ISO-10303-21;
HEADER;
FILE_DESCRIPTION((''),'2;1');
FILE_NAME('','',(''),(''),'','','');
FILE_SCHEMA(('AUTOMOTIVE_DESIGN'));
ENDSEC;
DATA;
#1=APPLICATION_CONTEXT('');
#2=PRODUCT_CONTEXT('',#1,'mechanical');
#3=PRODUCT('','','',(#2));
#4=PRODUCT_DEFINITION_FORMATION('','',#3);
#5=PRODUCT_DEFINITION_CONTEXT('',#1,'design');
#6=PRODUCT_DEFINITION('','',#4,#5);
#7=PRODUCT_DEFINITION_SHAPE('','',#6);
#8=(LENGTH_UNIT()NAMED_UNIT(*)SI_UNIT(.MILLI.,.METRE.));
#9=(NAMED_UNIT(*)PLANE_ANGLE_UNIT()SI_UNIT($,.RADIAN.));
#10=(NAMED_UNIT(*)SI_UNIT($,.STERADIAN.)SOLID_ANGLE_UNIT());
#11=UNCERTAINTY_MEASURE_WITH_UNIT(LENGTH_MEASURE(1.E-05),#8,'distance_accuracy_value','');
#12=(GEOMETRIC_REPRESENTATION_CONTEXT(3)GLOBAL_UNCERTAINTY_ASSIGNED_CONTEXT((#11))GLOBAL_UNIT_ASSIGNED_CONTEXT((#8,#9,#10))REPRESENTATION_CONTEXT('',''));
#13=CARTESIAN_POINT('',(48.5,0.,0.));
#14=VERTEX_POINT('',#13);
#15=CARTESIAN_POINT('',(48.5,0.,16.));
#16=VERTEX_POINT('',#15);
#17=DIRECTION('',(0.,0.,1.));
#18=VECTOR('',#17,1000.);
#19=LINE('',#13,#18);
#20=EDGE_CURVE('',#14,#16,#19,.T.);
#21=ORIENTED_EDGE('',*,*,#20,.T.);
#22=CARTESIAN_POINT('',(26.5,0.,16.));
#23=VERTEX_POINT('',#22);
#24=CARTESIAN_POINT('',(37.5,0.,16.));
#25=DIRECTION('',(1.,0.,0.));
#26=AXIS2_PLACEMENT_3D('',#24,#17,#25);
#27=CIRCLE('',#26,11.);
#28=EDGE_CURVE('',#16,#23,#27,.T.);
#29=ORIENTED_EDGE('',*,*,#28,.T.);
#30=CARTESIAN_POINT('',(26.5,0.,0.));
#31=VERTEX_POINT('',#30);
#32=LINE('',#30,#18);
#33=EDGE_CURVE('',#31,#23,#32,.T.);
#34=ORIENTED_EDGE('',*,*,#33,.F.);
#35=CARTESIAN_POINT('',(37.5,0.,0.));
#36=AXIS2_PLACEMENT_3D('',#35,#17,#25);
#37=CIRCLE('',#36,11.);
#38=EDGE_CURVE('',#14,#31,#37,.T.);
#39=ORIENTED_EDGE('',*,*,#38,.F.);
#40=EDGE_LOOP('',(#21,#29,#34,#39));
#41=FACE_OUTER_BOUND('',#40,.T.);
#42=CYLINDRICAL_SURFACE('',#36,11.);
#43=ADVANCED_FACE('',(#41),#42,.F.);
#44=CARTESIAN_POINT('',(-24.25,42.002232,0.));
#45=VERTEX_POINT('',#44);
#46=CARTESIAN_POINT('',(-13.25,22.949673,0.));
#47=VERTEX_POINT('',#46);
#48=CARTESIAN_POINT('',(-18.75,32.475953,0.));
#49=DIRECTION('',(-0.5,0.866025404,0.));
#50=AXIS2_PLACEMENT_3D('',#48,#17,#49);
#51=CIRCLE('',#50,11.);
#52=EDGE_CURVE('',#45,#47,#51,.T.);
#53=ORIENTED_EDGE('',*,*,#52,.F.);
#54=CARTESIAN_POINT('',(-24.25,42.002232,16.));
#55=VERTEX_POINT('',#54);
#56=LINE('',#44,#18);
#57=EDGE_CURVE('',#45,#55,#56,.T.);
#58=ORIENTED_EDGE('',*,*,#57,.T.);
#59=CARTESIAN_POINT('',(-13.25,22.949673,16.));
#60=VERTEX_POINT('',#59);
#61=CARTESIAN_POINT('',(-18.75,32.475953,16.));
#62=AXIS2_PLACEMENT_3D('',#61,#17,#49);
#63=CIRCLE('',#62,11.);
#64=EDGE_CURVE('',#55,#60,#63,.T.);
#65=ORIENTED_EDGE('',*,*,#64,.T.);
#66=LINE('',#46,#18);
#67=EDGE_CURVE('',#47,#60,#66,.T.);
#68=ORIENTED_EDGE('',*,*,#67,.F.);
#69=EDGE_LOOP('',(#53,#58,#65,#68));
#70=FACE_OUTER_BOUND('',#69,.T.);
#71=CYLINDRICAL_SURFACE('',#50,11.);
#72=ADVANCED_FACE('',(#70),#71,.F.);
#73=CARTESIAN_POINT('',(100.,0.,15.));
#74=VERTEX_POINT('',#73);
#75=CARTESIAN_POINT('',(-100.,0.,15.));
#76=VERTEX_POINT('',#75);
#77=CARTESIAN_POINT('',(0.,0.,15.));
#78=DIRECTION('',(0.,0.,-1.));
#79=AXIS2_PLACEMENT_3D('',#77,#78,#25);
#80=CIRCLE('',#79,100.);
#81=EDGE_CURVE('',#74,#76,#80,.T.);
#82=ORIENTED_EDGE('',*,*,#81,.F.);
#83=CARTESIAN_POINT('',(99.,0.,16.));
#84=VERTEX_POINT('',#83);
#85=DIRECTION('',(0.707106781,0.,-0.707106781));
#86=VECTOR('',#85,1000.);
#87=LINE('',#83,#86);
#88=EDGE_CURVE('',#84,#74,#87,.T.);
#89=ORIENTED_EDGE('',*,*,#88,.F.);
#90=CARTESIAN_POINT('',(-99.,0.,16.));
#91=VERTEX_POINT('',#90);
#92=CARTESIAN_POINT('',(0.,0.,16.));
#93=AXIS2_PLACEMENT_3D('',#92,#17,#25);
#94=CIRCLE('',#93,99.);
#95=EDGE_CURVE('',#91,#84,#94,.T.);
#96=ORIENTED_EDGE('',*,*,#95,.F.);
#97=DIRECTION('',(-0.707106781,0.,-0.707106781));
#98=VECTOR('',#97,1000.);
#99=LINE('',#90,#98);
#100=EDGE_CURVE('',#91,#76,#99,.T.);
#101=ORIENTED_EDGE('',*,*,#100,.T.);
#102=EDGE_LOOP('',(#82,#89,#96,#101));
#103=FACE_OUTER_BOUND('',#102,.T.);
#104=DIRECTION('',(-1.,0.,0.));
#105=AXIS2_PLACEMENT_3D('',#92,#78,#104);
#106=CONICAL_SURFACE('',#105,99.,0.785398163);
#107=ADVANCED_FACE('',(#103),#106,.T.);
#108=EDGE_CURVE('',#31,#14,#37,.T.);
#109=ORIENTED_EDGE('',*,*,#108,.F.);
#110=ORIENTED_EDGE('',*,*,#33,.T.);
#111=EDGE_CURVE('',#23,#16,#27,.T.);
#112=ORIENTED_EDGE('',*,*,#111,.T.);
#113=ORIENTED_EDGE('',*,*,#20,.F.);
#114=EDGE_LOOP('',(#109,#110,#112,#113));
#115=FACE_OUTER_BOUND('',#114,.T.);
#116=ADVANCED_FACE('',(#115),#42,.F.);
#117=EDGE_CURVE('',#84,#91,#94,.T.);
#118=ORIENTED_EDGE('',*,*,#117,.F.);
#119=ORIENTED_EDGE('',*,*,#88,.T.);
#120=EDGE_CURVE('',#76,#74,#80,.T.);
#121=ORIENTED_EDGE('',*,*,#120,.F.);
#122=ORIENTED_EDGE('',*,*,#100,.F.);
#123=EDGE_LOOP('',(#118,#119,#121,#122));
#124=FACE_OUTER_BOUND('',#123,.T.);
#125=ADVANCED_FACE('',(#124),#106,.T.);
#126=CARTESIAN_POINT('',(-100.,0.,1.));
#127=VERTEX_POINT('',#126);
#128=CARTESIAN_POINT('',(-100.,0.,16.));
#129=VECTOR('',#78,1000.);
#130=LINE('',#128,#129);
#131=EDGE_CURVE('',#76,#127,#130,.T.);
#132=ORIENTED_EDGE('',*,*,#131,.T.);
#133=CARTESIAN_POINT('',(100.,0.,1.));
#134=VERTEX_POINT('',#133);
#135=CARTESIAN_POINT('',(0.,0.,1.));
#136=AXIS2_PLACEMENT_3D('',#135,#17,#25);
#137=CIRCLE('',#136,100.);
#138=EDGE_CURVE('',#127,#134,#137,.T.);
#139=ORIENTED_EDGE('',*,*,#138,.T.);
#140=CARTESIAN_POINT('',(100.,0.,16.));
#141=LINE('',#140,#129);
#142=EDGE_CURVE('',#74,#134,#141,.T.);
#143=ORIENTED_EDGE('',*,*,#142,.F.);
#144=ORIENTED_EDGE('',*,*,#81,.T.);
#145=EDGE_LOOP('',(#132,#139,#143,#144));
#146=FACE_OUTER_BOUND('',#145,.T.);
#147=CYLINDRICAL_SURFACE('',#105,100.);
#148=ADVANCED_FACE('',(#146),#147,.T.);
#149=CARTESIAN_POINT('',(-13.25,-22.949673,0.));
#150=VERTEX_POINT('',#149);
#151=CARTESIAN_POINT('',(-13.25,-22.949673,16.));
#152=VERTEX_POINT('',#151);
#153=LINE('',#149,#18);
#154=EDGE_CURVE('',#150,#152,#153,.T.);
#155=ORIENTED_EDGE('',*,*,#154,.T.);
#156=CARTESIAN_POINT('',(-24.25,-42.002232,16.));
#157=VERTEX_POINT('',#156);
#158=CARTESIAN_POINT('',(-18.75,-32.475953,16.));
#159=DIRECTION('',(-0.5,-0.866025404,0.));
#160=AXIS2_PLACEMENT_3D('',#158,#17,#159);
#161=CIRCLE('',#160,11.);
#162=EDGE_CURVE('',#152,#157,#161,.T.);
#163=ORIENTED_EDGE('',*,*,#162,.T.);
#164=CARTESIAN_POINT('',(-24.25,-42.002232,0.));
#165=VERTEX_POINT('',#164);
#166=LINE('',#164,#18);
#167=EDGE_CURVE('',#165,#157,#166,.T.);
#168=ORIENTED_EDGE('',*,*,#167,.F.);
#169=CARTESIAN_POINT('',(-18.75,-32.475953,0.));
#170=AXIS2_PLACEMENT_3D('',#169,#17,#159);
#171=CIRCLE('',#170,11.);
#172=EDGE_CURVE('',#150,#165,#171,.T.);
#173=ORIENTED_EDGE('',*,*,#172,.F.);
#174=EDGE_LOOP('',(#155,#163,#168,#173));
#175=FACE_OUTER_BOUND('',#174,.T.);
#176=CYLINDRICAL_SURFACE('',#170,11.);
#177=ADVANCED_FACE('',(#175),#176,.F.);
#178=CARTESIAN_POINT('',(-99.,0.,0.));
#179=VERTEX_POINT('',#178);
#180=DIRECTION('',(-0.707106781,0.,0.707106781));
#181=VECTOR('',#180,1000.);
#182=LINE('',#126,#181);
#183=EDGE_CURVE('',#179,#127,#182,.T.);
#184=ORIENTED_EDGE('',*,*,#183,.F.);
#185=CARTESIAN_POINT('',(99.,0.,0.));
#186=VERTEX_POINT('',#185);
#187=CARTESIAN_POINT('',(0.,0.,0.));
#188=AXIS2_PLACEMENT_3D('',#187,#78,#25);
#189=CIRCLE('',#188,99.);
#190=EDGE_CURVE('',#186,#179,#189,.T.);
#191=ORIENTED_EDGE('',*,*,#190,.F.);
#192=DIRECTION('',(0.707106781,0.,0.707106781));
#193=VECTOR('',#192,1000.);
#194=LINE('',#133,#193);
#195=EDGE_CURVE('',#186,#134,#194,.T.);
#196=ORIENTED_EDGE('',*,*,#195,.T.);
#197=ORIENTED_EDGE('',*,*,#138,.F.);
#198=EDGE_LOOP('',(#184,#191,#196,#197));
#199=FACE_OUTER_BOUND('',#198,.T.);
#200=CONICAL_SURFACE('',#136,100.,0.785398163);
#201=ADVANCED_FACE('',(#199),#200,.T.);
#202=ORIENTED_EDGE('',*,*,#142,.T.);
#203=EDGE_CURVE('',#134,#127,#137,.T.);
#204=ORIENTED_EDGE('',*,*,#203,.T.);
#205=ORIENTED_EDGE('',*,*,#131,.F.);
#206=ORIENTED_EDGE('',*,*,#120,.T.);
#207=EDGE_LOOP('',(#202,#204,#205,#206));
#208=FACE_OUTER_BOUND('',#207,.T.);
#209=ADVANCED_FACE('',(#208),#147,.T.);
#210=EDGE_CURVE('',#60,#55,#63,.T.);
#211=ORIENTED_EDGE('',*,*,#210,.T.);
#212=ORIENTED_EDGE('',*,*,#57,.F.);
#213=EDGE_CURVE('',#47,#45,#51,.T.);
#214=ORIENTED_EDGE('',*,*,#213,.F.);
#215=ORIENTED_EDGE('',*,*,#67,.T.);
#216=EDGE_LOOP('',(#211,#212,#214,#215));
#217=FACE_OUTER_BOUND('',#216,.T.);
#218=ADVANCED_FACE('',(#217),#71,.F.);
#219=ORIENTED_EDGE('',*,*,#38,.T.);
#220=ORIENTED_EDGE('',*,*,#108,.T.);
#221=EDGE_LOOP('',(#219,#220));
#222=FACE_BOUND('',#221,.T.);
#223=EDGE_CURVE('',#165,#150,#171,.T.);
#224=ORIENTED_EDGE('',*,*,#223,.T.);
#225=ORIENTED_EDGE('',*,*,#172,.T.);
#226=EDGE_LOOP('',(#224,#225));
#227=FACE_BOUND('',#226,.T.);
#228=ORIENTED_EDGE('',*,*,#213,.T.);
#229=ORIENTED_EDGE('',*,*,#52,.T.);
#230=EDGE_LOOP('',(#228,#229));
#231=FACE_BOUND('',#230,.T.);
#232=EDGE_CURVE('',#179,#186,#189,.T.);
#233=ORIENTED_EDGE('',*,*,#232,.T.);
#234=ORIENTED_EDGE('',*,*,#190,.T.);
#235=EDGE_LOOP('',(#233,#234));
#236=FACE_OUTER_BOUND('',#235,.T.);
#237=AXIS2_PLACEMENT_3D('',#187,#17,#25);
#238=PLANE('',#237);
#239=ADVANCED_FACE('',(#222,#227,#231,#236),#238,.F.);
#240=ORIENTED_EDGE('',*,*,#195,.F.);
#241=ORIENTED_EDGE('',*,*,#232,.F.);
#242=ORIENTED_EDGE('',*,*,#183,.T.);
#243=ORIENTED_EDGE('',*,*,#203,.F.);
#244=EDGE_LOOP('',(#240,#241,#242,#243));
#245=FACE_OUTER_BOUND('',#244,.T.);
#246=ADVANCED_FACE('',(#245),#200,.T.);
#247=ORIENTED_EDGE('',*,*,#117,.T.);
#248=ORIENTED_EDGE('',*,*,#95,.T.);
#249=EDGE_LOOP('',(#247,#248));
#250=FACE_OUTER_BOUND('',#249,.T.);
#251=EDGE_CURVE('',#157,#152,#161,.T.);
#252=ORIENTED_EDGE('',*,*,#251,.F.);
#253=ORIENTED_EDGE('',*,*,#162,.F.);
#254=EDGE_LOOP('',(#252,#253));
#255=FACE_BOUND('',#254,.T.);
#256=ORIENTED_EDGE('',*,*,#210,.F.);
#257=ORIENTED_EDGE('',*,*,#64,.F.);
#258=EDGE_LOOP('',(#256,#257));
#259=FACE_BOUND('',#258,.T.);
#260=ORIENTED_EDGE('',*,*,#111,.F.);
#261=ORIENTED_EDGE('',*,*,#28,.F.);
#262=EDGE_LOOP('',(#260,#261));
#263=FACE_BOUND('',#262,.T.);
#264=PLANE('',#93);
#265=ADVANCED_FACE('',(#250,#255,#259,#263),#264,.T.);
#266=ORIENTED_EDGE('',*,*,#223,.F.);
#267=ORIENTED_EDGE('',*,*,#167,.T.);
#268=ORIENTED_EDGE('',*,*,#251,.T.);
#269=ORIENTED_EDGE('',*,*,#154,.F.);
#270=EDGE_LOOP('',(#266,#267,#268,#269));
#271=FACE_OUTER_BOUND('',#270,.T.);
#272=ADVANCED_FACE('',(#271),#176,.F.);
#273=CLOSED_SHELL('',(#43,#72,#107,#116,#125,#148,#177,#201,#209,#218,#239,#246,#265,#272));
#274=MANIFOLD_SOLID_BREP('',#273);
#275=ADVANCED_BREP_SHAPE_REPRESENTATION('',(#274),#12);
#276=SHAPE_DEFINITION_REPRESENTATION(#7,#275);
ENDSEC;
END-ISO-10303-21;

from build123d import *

# Parameters (mm, degrees)
SKETCH1_R           = 100
BOSS_EXTRUDE1_DEPTH = 16
SKETCH2_R           = 11
CUT_EXTRUDE1_DEPTH  = 143.323574997
CIRPATTERN1_COUNT   = 3
CHAMFER1_SIZE       = 1


with BuildPart() as part:
    # Sketch1 → Boss-Extrude1 (new body)
    with BuildSketch(Plane.XY):
        Circle(SKETCH1_R)
    extrude(amount=BOSS_EXTRUDE1_DEPTH)

    # Sketch2 → Cut-Extrude1 (cut, through all)
    with BuildSketch(Plane.XY.offset(16)):
        with Locations((37.5, 0)):
            Circle(SKETCH2_R)
    cut_extrude1 = extrude(amount=-CUT_EXTRUDE1_DEPTH, mode=Mode.SUBTRACT)

    # CirPattern1: Cut-Extrude1 ×3 about axis
    cirpattern1_axis = Axis((0, 0, 0), (0, 0, 1))
    for i in range(1, CIRPATTERN1_COUNT):
        add(cut_extrude1.rotate(cirpattern1_axis, i * 360 / CIRPATTERN1_COUNT), mode=Mode.SUBTRACT)

    # Chamfer1
    chamfer1_edges = [part.edges().sort_by_distance(p)[0] for p in [
        (-100, 0, 0),
        (-100, 0, 16),
    ]]
    chamfer(chamfer1_edges, length=CHAMFER1_SIZE)


solid = part.part
